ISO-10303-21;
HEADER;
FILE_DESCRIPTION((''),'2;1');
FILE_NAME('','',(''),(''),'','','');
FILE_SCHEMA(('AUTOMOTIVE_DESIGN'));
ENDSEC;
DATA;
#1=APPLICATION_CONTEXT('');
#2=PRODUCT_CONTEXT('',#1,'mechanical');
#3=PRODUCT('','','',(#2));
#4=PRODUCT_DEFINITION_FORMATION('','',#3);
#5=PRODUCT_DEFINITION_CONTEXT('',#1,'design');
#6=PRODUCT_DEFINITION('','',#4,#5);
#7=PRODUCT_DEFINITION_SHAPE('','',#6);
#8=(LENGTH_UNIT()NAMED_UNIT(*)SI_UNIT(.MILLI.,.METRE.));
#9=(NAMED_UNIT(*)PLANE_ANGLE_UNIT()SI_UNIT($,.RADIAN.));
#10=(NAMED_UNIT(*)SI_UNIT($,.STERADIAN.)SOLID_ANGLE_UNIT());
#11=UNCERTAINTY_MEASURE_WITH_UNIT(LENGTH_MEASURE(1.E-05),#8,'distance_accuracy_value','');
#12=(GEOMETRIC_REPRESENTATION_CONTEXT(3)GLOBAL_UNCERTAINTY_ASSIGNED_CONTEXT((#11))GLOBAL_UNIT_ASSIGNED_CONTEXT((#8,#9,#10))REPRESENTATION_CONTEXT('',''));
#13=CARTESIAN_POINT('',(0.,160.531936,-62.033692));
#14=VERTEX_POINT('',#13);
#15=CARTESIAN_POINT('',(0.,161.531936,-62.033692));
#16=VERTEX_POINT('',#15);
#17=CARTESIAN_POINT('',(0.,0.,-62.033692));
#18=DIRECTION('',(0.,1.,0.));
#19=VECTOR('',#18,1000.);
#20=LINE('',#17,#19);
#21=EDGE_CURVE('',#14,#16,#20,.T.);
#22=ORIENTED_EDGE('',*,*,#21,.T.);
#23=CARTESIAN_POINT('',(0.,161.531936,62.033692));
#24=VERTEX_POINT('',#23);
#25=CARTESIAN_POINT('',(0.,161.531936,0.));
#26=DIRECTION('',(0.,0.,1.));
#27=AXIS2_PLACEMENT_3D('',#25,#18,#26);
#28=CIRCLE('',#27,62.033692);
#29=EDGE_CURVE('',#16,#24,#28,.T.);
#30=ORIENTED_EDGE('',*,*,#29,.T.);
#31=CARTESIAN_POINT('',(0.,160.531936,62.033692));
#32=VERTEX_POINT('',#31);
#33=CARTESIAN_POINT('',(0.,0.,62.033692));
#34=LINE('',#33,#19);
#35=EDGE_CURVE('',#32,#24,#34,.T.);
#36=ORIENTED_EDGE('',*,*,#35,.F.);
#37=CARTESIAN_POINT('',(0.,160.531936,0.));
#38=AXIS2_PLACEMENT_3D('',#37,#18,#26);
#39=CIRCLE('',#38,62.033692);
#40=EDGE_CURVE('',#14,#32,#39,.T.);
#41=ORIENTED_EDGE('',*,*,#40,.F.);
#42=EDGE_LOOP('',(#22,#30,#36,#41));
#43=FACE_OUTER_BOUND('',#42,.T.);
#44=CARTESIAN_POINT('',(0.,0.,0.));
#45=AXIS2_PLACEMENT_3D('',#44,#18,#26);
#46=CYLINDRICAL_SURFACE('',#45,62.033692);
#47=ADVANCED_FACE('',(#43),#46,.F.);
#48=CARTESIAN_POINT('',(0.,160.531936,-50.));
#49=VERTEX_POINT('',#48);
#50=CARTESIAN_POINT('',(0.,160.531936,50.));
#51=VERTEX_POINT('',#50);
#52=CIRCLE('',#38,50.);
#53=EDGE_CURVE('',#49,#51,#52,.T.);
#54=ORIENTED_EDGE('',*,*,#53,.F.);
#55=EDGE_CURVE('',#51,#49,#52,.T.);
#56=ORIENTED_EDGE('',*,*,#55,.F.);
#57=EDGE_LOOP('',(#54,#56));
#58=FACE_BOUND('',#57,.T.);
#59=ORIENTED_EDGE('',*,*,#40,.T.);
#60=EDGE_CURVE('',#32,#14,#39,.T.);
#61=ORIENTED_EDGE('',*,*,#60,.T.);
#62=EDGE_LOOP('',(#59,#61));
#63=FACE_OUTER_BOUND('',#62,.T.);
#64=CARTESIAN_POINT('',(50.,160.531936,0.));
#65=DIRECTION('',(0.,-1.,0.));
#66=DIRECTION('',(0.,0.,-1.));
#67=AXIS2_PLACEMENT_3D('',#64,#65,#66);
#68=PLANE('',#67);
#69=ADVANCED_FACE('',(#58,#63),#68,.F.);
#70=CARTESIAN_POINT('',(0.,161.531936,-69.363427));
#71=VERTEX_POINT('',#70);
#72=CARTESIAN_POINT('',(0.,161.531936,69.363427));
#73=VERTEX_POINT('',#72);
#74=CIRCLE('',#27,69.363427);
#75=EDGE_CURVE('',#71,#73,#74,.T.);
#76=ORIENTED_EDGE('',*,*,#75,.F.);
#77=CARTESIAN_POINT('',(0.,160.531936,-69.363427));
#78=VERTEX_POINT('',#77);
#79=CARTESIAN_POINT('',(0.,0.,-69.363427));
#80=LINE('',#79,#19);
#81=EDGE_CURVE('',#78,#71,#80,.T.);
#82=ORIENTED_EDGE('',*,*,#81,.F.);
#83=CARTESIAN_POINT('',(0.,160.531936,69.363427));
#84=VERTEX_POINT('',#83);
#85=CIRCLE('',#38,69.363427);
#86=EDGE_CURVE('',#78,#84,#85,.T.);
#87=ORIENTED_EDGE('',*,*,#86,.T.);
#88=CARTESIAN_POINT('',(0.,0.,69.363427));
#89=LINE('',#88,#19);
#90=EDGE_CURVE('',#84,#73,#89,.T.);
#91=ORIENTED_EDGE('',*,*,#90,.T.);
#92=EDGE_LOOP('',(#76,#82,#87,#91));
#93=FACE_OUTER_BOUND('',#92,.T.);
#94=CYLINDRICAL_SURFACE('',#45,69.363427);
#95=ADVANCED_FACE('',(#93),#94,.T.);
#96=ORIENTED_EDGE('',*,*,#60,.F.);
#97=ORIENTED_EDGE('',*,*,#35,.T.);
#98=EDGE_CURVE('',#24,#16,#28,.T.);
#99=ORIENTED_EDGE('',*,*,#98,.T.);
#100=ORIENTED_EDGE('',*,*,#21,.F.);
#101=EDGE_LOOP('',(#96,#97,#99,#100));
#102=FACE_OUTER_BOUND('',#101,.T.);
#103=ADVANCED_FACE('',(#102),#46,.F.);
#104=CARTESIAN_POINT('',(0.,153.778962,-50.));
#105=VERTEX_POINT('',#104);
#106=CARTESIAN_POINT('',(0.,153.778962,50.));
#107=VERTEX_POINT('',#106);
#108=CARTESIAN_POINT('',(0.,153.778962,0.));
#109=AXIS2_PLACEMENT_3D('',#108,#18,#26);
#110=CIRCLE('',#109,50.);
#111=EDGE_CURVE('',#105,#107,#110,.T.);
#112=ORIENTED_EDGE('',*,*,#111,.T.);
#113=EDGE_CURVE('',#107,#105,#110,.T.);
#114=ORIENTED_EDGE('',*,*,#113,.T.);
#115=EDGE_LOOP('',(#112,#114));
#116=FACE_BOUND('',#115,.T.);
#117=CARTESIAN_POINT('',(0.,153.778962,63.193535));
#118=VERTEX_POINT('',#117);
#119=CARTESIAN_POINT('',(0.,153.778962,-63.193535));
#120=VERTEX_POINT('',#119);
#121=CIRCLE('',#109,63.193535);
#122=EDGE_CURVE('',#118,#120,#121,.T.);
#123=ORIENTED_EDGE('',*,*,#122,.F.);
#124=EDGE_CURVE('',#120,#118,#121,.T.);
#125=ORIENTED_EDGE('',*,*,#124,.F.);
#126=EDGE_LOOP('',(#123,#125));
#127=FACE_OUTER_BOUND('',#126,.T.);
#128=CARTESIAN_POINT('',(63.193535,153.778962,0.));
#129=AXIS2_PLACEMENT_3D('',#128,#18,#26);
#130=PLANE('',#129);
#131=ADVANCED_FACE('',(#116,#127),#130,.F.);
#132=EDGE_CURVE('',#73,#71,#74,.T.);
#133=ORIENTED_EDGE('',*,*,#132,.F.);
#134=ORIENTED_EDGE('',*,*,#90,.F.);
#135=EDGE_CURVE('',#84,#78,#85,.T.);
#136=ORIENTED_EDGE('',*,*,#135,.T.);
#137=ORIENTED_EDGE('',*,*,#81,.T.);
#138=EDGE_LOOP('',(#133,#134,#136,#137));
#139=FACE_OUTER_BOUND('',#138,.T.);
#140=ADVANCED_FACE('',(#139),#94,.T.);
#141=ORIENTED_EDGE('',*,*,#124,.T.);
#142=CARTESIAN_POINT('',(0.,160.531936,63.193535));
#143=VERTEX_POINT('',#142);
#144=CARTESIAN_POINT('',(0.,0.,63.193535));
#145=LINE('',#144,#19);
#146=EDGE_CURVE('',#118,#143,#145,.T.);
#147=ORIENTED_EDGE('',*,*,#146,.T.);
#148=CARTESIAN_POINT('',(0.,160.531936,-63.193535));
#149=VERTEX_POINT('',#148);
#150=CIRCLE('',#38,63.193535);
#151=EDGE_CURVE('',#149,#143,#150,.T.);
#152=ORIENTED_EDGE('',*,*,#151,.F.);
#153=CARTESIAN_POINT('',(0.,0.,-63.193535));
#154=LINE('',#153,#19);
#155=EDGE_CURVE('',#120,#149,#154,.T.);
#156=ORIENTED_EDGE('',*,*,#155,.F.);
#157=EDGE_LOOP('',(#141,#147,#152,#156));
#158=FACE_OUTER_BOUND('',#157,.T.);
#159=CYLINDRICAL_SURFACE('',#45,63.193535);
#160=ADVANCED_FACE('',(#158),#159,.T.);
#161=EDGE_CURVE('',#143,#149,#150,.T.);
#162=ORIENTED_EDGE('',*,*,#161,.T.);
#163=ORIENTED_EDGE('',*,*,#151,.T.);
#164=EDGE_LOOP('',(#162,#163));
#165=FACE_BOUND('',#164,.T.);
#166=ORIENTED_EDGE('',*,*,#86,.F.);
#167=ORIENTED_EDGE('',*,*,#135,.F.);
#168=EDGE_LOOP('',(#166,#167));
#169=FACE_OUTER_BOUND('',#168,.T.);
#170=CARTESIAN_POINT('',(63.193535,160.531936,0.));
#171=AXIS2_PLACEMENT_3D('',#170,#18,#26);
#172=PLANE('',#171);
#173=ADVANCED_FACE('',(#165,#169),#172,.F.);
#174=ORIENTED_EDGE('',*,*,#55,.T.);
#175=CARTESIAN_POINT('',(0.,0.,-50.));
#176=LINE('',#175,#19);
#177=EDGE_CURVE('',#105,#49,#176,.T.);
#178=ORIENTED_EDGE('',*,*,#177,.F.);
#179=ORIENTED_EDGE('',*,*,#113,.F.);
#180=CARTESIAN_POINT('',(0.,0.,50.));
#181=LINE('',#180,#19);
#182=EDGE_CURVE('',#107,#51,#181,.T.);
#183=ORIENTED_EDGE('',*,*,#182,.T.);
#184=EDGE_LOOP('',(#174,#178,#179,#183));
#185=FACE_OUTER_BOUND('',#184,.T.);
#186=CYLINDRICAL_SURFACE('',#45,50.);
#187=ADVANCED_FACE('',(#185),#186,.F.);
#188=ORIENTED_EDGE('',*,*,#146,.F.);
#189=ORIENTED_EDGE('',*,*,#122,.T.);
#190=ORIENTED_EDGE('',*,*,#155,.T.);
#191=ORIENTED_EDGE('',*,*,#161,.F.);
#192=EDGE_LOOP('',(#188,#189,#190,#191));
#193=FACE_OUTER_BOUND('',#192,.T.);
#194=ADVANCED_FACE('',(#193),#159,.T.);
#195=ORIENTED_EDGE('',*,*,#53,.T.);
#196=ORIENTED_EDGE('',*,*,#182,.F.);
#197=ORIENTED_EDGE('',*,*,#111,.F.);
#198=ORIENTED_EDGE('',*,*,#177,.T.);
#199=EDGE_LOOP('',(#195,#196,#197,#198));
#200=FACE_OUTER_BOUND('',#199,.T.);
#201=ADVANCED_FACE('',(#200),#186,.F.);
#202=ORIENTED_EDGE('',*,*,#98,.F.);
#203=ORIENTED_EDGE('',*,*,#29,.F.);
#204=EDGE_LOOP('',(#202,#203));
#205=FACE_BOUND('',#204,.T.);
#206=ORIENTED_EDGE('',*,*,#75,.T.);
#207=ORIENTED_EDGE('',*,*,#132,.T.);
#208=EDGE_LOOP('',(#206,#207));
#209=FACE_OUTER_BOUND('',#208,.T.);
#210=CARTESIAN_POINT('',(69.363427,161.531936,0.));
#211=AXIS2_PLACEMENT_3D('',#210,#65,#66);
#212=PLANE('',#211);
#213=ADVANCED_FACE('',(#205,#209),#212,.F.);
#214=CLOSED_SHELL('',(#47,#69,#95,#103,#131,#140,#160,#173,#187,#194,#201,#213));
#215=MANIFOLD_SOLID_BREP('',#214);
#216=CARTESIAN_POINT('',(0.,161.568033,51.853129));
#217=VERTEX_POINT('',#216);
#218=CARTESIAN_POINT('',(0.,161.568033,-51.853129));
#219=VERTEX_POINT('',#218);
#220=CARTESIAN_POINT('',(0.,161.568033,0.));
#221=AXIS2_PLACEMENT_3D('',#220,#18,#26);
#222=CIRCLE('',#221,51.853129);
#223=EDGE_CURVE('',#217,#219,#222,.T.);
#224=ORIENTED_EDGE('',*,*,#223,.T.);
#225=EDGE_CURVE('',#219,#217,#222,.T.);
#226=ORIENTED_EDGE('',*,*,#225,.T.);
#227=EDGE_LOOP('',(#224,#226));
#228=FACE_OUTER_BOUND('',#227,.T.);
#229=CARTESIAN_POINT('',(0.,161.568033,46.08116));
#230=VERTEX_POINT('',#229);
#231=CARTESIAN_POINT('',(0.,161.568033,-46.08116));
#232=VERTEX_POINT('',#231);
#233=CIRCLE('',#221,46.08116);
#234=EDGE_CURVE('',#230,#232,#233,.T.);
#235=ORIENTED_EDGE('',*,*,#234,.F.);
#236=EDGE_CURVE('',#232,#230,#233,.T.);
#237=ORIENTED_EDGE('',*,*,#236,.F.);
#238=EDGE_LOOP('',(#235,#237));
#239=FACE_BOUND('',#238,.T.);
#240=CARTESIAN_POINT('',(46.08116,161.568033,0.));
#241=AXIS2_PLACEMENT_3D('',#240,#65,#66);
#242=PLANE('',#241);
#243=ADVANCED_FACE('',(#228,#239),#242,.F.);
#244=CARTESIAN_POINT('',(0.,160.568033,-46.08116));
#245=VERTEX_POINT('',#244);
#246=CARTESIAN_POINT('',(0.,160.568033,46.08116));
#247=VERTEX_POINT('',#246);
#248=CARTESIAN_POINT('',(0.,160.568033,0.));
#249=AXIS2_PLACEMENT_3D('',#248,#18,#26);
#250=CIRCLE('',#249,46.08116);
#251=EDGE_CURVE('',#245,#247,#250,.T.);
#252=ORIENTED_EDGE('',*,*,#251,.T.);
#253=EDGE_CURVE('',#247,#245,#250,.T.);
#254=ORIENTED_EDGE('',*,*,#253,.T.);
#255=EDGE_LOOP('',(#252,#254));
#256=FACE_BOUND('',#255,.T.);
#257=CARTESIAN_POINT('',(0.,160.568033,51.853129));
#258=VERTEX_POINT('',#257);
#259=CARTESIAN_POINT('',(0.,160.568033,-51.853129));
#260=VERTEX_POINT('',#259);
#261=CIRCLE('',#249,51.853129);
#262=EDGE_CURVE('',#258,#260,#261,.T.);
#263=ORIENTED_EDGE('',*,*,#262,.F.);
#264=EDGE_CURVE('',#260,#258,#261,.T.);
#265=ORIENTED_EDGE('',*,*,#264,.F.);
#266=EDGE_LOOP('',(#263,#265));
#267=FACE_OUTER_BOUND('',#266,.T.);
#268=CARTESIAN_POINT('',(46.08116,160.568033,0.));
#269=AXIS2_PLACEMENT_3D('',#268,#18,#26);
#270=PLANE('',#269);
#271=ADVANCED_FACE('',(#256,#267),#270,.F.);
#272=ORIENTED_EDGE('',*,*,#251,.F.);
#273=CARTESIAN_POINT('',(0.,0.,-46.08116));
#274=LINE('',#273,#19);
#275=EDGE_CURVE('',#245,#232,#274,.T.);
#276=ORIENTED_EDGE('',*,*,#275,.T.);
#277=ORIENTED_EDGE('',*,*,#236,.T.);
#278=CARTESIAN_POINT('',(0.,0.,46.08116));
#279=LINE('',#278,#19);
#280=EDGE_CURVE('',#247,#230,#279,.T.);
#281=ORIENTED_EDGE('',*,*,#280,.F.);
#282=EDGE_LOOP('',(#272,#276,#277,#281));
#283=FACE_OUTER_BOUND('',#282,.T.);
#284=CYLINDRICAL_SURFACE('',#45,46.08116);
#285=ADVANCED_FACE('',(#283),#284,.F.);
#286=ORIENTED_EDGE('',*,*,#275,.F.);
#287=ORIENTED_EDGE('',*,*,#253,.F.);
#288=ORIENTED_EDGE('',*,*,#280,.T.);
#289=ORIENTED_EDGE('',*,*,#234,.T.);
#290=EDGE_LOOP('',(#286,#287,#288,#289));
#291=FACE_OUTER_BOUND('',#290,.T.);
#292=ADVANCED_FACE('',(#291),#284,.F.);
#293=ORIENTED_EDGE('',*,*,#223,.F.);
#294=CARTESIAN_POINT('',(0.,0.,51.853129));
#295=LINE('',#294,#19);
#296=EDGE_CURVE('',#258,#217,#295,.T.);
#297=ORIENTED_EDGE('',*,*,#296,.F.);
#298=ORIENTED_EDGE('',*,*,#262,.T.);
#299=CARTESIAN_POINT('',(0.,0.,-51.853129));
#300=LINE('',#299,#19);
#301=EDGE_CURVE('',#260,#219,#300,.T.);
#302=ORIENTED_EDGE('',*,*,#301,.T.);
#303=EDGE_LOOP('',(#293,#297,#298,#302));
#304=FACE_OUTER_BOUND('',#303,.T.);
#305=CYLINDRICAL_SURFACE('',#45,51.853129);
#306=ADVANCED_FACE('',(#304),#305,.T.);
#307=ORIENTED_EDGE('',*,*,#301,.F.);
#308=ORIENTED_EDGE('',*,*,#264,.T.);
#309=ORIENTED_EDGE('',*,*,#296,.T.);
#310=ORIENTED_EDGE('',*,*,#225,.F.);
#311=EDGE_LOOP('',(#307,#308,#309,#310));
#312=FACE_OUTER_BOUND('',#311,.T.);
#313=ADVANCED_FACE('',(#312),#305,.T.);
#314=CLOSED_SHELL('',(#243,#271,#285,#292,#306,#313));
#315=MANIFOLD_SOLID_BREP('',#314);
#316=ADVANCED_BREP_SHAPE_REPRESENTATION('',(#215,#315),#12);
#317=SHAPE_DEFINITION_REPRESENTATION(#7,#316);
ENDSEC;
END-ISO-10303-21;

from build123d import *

# Parameters (mm, degrees)
SKETCH1_W = 5.771968746
SKETCH1_H = 1


with BuildPart() as part:
    # Sketch1 → Revolve1 (revolve)
    with BuildSketch(Plane.XY, mode=Mode.PRIVATE) as revolve1_sk:
        Polygon((63.193534924, 160.531936258), (69.363427474, 160.531936258), (69.363427474, 161.531936258), (62.033691631, 161.531936258), (62.033691631, 160.531936258), (50, 160.531936258), (50, 153.778962031), (63.193534924, 153.778962031), align=None)
        with Locations((48.9671445, 161.068033461)):
            Rectangle(SKETCH1_W, SKETCH1_H)
    revolve(revolve1_sk.sketch.rotate(Axis((0, 0, 0), (0, -1, 0)), 90), axis=Axis((0, 0, 0), (0, -1, 0)))


solid = part.part
